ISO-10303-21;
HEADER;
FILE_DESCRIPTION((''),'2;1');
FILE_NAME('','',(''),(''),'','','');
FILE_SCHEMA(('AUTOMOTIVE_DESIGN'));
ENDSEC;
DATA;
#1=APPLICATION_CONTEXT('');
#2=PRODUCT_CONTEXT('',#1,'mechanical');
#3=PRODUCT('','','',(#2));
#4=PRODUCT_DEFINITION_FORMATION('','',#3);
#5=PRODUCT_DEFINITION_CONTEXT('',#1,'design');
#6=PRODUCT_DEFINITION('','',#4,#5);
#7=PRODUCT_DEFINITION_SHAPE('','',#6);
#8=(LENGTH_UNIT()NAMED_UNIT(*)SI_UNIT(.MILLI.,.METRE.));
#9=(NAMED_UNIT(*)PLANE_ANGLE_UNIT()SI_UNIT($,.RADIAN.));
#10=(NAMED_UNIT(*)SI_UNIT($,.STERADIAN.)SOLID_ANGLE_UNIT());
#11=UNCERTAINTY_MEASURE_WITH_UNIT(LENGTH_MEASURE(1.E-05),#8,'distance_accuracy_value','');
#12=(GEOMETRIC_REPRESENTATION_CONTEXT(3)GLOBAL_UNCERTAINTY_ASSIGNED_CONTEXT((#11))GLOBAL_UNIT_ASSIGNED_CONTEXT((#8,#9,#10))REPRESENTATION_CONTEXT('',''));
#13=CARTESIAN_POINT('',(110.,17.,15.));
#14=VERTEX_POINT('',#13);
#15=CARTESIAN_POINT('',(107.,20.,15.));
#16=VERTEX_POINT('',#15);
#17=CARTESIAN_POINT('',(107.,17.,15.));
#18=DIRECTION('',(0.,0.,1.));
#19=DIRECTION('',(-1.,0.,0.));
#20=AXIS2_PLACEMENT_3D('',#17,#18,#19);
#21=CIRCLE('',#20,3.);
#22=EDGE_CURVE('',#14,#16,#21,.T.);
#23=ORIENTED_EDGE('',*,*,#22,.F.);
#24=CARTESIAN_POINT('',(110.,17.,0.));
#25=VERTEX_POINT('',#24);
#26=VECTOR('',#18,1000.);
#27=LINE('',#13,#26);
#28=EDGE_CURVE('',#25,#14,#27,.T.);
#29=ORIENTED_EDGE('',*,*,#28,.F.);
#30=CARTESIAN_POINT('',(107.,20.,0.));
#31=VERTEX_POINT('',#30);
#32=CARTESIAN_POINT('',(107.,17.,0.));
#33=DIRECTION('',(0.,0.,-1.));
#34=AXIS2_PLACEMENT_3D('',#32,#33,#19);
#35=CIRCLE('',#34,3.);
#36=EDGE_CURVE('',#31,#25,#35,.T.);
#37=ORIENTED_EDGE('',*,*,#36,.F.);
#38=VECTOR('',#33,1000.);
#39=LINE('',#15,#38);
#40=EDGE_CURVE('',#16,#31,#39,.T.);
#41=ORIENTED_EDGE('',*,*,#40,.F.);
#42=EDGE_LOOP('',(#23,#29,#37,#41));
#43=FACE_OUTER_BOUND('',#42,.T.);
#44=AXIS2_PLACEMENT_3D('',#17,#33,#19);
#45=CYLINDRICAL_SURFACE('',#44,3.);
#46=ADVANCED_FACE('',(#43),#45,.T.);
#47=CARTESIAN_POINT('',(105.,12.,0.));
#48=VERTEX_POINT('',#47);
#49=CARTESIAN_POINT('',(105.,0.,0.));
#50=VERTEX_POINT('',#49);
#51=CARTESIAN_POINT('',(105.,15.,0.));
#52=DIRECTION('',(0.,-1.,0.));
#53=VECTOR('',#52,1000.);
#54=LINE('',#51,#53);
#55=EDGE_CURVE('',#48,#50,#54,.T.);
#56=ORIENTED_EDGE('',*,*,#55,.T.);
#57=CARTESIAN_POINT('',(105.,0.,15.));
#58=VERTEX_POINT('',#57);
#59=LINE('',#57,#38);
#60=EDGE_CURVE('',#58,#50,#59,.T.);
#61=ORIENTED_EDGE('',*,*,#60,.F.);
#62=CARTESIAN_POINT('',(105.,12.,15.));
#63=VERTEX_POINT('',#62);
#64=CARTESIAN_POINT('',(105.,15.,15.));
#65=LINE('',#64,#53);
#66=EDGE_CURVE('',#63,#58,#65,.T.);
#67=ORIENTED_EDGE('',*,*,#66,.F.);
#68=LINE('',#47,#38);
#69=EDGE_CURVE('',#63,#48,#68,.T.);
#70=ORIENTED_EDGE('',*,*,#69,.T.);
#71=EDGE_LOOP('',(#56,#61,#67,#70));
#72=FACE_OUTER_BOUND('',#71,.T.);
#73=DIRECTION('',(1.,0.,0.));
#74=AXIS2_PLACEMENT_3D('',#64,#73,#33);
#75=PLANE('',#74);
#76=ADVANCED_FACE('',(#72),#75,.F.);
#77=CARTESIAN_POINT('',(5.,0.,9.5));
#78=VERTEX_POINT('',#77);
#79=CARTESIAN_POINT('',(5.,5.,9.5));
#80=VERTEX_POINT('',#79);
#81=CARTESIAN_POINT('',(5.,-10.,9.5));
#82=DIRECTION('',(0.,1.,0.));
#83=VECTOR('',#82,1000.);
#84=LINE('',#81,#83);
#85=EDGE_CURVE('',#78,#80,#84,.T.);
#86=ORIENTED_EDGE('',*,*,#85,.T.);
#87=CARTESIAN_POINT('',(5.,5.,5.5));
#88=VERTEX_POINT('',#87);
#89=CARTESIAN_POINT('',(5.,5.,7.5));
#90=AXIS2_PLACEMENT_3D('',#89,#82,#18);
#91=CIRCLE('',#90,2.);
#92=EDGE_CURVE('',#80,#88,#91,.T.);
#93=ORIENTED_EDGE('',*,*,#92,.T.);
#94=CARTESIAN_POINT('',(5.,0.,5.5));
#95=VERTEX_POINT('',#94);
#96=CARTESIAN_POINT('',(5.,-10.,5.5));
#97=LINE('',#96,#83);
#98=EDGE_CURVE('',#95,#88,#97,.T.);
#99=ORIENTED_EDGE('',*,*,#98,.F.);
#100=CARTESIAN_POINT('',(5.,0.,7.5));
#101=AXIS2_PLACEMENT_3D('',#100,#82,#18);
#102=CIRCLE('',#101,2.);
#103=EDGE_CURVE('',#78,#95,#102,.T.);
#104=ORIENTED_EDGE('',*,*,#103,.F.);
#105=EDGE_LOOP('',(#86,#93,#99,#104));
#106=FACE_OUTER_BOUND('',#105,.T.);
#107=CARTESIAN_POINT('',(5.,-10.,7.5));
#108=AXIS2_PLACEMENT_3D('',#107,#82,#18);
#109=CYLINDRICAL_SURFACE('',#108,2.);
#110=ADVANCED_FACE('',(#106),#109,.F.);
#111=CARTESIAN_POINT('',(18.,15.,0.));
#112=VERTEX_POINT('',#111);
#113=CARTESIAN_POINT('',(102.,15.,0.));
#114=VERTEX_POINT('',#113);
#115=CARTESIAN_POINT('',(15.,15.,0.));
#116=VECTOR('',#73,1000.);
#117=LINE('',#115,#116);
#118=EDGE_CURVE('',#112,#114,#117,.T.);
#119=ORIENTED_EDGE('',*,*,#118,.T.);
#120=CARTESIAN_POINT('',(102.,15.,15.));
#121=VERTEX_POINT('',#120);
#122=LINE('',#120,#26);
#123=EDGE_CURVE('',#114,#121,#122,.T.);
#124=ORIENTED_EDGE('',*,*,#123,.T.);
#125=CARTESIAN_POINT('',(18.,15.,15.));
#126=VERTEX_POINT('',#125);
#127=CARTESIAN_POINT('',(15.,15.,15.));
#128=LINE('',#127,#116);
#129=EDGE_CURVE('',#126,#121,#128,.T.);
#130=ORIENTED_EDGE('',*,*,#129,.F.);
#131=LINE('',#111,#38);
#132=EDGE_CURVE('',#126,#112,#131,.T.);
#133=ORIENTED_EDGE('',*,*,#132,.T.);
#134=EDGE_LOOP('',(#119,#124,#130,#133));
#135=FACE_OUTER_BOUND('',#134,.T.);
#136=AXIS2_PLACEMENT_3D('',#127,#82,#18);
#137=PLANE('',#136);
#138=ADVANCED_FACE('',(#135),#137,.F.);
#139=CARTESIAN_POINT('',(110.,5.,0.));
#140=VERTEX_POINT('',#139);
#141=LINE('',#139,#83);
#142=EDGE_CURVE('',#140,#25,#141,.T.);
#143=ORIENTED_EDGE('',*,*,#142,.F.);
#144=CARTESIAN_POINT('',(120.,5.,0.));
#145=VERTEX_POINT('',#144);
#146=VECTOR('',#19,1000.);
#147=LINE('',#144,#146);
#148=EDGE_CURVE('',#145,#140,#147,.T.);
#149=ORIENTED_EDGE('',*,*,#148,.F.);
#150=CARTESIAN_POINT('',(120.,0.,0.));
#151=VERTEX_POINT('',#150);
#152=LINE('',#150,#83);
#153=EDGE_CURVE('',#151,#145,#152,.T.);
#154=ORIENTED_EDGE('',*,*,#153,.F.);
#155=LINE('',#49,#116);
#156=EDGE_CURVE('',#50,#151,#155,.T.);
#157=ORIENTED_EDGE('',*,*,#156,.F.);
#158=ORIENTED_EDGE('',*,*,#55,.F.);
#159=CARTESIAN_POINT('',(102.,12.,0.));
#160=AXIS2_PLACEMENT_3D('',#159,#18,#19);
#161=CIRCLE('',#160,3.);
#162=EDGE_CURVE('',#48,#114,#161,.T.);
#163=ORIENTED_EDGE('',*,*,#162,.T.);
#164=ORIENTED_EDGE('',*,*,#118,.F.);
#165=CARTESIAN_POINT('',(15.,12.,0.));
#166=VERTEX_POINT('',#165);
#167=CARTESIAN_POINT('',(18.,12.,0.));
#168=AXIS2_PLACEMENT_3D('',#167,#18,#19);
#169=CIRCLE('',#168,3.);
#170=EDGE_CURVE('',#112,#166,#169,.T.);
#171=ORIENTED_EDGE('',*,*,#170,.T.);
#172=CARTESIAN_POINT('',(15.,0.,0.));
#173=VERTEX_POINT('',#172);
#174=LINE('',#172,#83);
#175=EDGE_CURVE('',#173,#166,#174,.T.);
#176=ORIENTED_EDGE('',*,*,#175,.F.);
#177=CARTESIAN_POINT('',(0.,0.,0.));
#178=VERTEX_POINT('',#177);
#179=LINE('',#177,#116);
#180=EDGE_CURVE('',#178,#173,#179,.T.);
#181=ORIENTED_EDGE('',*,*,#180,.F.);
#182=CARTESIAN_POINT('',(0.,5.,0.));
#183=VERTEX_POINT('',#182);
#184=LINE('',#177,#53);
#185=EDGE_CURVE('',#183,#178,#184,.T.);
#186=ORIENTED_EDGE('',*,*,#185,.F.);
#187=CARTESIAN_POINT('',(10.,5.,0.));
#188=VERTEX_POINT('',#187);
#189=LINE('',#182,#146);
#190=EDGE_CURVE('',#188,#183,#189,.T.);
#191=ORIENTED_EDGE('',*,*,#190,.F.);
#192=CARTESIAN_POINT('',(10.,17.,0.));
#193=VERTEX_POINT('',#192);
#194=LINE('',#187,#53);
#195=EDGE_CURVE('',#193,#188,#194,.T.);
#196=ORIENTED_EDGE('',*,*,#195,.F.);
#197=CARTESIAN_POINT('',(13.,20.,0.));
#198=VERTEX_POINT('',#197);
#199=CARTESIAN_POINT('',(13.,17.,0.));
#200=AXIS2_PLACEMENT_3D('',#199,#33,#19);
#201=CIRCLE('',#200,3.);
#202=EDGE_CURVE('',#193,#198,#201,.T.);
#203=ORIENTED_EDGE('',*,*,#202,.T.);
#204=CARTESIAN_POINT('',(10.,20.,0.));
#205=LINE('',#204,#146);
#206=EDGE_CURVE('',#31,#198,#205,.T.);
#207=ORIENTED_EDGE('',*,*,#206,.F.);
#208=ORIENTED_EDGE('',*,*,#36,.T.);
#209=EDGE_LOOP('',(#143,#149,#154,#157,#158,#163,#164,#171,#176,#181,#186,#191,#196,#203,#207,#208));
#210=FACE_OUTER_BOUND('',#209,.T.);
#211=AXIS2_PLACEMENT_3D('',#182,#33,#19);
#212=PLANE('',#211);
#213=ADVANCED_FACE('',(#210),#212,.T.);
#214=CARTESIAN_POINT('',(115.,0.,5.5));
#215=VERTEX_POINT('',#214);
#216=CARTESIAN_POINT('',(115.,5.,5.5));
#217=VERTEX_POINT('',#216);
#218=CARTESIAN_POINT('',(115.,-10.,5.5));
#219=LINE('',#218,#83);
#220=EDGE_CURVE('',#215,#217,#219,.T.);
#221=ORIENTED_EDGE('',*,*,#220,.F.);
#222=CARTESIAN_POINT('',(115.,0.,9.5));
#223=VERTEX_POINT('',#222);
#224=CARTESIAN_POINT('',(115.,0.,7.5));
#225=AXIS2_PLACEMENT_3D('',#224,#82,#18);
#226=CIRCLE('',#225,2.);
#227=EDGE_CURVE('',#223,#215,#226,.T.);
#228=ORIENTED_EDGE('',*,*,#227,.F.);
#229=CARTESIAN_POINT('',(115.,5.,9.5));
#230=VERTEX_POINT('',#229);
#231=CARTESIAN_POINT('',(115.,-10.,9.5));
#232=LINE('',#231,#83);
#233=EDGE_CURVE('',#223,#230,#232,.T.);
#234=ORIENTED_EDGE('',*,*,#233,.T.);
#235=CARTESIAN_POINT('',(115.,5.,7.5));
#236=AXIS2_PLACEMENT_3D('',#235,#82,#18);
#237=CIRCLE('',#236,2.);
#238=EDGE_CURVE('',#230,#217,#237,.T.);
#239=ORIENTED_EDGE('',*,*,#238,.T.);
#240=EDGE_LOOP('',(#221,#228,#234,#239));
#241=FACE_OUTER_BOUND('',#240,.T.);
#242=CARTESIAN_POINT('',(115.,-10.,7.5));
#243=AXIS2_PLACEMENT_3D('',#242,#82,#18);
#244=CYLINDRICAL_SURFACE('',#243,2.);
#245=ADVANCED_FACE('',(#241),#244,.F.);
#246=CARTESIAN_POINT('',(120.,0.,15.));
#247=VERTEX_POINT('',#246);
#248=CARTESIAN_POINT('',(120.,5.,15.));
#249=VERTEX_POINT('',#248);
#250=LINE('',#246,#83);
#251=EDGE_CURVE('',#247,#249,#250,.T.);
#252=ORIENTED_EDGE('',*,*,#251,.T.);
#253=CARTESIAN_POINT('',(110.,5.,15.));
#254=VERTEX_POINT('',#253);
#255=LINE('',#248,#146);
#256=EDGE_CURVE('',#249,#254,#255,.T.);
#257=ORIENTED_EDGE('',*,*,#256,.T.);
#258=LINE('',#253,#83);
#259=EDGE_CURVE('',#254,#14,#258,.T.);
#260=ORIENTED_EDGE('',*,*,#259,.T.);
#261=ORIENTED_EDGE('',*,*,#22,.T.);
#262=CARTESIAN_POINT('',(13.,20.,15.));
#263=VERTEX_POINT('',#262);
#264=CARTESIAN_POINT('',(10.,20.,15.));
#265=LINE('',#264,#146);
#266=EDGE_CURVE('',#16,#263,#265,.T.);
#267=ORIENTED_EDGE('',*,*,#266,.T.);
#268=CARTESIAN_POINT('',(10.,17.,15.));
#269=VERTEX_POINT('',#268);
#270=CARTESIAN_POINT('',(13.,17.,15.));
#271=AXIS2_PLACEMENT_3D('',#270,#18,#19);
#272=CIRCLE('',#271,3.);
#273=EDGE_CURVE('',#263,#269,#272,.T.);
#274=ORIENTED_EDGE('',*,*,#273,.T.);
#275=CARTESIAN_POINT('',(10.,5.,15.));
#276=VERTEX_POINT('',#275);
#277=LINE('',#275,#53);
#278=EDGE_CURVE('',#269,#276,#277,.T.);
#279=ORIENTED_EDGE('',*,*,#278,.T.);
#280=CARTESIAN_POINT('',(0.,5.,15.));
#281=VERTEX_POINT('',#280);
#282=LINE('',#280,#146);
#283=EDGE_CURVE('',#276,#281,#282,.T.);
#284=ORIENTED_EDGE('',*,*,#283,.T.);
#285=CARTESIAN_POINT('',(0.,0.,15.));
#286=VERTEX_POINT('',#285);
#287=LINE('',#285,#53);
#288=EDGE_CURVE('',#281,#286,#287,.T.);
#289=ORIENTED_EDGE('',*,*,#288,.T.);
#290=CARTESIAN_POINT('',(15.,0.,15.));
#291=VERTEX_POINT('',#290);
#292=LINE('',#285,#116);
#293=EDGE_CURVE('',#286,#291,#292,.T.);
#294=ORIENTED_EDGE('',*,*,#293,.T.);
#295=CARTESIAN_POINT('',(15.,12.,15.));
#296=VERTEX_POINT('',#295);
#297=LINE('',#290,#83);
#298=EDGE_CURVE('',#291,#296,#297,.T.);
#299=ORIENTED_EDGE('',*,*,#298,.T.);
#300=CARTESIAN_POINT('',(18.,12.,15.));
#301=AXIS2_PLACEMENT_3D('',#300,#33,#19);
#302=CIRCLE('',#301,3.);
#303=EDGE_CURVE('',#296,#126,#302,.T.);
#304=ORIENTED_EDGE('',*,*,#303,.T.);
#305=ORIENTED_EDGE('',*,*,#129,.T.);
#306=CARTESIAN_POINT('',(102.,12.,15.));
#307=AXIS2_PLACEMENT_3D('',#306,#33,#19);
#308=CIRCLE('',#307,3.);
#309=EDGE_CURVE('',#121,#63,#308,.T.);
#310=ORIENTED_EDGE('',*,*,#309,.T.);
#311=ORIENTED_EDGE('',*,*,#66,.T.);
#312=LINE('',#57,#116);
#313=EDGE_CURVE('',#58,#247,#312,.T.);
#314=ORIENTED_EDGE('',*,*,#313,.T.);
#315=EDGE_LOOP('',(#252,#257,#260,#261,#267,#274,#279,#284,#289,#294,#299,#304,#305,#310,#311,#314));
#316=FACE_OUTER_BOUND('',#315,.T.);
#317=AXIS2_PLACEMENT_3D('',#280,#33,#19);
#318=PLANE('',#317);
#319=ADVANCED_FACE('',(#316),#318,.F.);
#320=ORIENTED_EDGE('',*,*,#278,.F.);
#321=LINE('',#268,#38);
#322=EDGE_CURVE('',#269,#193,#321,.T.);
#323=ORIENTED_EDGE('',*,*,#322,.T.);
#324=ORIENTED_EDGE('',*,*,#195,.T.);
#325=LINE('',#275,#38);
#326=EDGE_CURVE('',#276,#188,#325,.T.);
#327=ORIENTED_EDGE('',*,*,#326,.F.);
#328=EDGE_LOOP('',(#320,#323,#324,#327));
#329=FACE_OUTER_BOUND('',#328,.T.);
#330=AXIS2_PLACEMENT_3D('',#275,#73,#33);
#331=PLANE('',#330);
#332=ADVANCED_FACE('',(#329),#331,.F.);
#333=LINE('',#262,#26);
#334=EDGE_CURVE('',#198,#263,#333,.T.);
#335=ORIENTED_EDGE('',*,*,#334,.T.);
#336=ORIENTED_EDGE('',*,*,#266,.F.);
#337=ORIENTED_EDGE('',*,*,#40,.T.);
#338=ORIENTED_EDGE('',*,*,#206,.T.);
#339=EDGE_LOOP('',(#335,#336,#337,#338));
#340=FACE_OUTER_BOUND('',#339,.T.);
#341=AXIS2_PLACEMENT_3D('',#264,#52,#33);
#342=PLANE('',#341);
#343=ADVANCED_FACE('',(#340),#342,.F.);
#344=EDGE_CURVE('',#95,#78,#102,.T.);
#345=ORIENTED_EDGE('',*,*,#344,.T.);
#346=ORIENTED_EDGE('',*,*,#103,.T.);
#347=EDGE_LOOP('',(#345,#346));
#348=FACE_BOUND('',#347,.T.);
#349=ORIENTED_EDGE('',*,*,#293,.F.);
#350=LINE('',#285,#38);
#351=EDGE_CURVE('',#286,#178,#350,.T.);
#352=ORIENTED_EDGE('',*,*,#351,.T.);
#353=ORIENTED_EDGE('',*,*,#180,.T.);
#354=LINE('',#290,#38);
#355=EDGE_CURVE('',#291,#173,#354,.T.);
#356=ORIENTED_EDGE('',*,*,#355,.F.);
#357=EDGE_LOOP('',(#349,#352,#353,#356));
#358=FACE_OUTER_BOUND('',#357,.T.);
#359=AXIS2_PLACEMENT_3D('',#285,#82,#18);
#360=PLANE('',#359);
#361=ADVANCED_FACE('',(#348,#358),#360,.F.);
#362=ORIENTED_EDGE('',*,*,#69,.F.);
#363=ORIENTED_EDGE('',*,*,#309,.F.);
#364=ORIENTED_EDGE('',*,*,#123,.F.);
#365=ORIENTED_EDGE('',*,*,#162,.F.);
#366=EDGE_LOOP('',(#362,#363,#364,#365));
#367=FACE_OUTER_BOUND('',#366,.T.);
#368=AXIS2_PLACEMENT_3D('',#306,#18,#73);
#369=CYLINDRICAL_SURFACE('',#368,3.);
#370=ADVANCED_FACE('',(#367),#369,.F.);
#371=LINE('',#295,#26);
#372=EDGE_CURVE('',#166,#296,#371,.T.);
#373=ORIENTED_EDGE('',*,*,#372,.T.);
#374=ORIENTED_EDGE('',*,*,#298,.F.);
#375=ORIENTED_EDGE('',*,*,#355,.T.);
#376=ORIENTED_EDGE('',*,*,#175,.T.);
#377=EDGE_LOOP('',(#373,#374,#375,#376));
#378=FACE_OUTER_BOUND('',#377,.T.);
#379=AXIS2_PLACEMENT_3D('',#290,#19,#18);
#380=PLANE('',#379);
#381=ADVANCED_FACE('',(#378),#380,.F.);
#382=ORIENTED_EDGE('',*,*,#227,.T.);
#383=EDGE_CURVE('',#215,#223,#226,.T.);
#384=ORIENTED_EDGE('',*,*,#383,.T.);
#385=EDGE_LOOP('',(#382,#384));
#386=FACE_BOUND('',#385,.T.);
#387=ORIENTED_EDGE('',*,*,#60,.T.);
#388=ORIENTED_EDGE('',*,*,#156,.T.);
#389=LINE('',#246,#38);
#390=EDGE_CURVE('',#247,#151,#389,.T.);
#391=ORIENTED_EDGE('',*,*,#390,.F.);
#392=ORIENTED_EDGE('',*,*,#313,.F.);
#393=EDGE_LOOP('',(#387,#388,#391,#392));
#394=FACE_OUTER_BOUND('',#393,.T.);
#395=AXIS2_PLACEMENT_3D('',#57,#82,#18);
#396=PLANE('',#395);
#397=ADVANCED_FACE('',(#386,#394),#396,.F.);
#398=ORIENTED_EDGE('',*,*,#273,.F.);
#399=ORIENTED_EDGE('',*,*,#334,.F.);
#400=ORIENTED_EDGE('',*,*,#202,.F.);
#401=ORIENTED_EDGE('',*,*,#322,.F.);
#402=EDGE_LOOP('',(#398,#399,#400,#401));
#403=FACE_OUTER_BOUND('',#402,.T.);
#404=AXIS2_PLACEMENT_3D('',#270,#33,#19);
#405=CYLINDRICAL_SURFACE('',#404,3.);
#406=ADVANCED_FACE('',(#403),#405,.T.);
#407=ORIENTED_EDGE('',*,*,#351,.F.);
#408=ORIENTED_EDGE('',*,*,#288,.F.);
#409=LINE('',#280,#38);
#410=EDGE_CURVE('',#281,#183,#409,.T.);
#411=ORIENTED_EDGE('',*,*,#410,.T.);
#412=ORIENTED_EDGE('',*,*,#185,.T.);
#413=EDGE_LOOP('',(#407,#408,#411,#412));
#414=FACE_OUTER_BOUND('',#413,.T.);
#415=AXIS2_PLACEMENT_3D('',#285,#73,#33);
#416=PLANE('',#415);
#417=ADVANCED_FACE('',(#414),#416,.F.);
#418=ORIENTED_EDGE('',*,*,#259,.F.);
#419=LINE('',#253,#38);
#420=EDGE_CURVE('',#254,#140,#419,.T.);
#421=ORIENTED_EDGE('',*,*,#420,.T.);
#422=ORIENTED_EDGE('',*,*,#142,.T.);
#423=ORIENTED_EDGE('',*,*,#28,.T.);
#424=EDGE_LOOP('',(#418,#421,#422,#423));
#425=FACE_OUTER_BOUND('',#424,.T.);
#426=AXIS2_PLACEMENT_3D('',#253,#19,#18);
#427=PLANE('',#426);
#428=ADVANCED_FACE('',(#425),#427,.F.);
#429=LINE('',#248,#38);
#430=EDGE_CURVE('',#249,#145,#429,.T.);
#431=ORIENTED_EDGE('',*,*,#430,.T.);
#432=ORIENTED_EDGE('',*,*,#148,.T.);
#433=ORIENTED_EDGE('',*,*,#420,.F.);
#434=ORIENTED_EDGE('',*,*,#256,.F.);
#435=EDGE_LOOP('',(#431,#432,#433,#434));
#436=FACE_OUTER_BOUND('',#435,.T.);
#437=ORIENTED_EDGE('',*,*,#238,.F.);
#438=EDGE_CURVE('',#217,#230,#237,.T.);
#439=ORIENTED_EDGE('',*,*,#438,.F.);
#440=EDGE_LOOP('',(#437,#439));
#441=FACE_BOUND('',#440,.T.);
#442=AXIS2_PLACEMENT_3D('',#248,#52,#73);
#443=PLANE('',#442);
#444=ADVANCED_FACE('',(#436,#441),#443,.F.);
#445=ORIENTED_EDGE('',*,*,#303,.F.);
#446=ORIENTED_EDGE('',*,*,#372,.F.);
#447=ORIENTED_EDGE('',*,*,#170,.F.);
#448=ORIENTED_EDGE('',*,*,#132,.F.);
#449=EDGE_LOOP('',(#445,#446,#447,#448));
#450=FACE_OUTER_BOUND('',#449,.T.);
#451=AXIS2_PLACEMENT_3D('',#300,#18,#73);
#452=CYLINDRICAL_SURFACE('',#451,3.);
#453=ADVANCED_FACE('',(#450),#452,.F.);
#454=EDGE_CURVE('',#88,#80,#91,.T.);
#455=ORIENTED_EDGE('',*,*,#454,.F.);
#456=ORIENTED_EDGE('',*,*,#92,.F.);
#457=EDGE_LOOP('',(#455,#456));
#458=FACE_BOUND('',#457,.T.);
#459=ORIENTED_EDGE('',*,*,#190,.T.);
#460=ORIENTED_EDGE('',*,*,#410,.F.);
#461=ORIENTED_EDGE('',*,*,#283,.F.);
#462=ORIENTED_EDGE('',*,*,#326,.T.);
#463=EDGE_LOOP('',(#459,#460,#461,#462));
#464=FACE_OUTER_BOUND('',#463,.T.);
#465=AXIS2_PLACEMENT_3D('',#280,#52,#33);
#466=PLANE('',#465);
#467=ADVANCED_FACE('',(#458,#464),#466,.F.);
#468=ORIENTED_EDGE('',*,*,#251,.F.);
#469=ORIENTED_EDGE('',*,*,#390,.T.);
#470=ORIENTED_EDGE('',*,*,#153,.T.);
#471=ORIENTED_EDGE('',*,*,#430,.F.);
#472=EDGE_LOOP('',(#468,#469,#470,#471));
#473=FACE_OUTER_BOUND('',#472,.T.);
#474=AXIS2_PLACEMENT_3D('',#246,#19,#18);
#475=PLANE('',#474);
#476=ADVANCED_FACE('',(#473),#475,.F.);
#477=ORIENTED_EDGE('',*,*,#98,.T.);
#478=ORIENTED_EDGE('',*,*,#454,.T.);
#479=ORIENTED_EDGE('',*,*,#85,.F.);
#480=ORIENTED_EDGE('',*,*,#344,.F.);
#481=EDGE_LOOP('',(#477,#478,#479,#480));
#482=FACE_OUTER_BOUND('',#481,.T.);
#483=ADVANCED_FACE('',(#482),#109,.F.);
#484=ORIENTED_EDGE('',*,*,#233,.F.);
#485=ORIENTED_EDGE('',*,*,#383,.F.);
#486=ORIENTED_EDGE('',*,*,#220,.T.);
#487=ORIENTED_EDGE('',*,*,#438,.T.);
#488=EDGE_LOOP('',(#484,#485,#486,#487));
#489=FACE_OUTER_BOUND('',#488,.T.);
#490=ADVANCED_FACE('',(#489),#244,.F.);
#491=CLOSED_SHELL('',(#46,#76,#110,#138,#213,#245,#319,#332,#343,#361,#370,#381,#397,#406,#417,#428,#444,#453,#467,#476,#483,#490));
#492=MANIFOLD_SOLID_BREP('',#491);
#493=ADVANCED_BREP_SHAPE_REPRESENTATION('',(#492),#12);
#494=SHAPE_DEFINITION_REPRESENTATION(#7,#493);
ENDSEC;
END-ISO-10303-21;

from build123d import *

# Parameters (mm, degrees)
EXTRUDE_1_DEPTH     = 15
SKETCH_2_R          = 2
CUT_EXTRUDE_1_DEPTH = 15
FILLET_1_R          = 3


with BuildPart() as part:
    # 草图1 → 凸台-拉伸1 (new body)
    with BuildSketch(Plane.XY):
        Polygon((0, 0), (15, 0), (15, 15), (105, 15), (105, 0), (120, 0), (120, 5), (110, 5), (110, 20), (10, 20), (10, 5), (0, 5), align=None)
    extrude(amount=EXTRUDE_1_DEPTH)

    # 草图2 → 切除-拉伸1 (cut)
    with BuildSketch(Plane(origin=(0, 5, 0), x_dir=(1, 0, 0), z_dir=(0, 1, 0))):
        with Locations(Location((5, -7.5, 0), (0, 0, 270))):
            Circle(SKETCH_2_R)
        with Locations(Location((115, -7.5, 0), (0, 0, 270))):
            Circle(SKETCH_2_R)
    extrude(amount=-CUT_EXTRUDE_1_DEPTH, mode=Mode.SUBTRACT)

    # 圆角1
    fillet_1_edges = [part.edges().sort_by_distance(p)[0] for p in [
        (10, 20, 7.5),
        (110, 20, 7.5),
        (105, 15, 7.5),
        (15, 15, 7.5),
    ]]
    fillet(fillet_1_edges, radius=FILLET_1_R)


solid = part.part
